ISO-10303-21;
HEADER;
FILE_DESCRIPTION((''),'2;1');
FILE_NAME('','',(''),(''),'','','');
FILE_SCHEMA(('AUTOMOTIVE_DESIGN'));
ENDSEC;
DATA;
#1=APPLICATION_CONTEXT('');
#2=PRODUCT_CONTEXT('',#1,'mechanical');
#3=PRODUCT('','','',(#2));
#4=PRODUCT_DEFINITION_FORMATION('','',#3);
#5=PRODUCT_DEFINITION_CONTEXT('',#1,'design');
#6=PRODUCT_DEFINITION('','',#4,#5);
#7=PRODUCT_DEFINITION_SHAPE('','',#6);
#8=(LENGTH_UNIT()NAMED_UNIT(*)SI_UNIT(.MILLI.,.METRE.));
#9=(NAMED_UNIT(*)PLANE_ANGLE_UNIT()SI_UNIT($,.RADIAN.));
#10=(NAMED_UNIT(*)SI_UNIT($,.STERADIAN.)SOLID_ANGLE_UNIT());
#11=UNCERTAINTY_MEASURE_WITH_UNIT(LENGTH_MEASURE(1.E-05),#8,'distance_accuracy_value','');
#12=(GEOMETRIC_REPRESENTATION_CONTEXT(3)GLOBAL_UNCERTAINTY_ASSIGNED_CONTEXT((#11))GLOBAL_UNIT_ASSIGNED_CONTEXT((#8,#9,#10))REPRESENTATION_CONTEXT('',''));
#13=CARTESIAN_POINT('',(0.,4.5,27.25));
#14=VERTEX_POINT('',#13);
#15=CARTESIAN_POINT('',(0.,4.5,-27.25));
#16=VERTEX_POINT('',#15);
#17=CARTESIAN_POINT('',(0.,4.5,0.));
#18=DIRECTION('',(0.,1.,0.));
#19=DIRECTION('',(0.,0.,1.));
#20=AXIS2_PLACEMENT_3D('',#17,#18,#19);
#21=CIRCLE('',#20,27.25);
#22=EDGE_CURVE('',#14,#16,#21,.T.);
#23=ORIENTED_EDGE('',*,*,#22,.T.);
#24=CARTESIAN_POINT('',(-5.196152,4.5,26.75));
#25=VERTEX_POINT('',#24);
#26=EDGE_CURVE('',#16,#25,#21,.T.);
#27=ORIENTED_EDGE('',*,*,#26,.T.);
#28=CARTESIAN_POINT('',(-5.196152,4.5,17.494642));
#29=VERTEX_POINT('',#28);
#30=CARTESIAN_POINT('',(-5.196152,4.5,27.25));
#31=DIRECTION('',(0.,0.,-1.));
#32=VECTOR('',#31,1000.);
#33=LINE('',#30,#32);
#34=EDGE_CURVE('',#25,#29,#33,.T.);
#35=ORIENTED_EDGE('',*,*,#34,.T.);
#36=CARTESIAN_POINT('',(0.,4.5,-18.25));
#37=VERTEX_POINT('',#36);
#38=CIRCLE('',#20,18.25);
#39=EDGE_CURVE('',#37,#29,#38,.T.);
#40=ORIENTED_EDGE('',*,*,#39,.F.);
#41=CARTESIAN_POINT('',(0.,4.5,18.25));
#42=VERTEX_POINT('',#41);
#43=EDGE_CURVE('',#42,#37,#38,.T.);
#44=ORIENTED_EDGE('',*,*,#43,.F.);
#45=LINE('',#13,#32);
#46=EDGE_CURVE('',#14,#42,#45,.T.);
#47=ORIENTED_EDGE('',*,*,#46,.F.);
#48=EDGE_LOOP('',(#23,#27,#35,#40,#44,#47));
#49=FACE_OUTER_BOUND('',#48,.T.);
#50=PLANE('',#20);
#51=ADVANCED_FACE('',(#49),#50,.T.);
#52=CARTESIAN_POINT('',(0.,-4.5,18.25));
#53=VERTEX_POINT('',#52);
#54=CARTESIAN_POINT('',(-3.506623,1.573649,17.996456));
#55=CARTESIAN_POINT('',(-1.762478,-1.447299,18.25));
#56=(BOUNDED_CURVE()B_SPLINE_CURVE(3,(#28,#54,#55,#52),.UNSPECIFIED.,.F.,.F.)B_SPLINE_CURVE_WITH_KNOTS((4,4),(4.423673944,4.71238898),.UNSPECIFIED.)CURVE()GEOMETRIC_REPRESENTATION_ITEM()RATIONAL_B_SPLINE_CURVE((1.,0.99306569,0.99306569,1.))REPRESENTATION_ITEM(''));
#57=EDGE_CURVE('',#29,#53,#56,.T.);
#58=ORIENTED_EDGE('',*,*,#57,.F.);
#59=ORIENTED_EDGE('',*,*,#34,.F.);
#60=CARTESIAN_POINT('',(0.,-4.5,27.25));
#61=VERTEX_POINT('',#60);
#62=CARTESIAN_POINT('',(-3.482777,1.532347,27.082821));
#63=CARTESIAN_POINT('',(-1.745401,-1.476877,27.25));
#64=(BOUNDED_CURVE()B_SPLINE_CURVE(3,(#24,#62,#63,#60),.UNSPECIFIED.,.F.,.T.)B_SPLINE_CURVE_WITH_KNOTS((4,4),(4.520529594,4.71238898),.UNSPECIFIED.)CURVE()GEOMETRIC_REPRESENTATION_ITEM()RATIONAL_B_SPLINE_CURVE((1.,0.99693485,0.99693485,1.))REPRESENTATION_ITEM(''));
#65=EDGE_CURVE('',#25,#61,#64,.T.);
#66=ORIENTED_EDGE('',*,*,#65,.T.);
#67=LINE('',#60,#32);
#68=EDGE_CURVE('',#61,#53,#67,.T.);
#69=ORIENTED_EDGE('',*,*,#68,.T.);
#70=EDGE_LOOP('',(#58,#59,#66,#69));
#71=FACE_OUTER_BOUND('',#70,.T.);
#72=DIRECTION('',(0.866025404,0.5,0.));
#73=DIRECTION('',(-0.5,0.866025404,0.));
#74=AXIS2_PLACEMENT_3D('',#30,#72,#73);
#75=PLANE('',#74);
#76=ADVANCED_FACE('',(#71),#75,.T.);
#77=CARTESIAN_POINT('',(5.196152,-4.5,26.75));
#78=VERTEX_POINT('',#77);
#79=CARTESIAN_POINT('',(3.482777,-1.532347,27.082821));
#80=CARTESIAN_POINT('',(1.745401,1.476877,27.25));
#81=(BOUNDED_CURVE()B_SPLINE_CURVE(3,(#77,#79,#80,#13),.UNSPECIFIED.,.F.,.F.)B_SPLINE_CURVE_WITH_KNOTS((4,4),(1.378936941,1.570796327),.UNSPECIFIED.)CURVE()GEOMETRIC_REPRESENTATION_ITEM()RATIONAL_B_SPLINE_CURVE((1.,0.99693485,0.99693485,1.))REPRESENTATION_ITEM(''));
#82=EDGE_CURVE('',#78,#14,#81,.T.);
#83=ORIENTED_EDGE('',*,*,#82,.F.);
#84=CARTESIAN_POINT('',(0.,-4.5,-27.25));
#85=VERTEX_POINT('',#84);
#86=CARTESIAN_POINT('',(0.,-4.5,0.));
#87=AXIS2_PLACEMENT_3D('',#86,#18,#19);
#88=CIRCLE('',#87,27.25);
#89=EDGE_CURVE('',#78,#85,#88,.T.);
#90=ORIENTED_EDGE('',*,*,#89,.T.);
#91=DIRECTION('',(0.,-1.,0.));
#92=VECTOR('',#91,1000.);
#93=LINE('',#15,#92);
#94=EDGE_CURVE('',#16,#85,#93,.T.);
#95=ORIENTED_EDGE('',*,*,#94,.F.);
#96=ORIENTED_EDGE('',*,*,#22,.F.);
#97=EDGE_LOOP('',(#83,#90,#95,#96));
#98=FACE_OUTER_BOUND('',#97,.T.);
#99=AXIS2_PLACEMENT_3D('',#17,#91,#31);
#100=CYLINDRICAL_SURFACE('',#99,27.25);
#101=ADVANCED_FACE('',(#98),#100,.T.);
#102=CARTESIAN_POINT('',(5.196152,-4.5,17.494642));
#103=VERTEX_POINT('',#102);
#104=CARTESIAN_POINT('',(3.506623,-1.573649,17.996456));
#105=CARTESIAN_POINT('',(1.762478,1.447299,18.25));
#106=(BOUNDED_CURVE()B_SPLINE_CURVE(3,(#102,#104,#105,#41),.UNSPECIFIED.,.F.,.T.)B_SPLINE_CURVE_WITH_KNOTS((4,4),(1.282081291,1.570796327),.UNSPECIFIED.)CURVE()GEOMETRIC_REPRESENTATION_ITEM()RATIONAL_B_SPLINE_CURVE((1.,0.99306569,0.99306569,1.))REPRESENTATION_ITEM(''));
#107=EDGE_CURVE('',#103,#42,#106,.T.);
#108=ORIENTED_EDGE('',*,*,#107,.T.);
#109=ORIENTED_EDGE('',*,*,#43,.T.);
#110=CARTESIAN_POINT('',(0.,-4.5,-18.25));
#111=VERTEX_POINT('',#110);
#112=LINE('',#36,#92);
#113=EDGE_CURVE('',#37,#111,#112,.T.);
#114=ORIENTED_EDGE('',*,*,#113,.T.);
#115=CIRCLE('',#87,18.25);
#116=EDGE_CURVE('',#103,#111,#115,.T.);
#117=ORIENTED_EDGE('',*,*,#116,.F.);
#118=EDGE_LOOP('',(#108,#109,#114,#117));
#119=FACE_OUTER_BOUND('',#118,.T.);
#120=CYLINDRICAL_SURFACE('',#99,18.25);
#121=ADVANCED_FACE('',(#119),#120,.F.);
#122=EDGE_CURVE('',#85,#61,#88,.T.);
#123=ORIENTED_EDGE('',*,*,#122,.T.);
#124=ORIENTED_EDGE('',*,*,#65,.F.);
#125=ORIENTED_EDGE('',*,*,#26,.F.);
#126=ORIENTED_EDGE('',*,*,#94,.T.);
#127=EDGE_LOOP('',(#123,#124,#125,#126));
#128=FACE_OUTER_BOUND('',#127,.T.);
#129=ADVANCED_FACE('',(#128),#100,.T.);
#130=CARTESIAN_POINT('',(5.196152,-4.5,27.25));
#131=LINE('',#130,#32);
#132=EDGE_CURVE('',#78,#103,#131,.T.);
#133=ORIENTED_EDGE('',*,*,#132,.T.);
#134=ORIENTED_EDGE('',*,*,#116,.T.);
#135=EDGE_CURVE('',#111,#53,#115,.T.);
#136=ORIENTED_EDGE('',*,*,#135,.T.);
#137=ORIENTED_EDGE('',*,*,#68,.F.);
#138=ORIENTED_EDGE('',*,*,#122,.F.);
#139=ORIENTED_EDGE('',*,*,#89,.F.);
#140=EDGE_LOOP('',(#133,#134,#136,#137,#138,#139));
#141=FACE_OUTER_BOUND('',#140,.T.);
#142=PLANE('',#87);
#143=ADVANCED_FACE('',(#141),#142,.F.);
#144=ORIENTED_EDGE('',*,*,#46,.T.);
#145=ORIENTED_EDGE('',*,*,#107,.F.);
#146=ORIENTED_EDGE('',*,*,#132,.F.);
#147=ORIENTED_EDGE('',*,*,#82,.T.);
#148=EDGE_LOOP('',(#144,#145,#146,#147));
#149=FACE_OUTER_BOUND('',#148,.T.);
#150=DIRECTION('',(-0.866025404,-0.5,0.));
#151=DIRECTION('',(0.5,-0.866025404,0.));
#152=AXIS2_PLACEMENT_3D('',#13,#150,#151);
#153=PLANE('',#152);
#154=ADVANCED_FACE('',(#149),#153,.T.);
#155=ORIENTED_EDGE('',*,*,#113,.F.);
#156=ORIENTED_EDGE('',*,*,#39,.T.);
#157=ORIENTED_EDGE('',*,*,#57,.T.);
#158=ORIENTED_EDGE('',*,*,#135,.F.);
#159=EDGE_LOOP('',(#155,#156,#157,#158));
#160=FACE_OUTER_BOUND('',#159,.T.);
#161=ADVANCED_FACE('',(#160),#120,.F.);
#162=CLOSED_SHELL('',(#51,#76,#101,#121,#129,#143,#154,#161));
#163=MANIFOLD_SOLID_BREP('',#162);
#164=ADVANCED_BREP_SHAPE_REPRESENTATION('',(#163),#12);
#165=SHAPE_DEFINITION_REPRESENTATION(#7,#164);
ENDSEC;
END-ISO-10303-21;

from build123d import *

# Parameters (mm, degrees)
SKETCH1_R           = 27.25
SKETCH1_R_2         = 18.25
BOSS_EXTRUDE1_DEPTH = 4.5
CUT_EXTRUDE1_DEPTH  = 39.799162362


with BuildPart() as part:
    # Sketch1 → Boss-Extrude1 (new, symmetric)
    with BuildSketch(Plane(origin=(0, 0, 0), x_dir=(1, 0, 0), z_dir=(0, 1, 0))):
        with Locations(Location((0, 0, 0), (0, 0, 270))):
            Circle(SKETCH1_R)
        with Locations(Location((0, 0, 0), (0, 0, 270))):
            Circle(SKETCH1_R_2, mode=Mode.SUBTRACT)
    extrude(amount=BOSS_EXTRUDE1_DEPTH, both=True)

    # Sketch2 → Cut-Extrude1 (cut, through all)
    with BuildSketch(Plane.XY):
        Polygon((0, 4.5), (-5.196152423, 4.5), (0, -4.5), (5.196152423, -4.5), align=None)
    extrude(amount=CUT_EXTRUDE1_DEPTH, mode=Mode.SUBTRACT)


solid = part.part
